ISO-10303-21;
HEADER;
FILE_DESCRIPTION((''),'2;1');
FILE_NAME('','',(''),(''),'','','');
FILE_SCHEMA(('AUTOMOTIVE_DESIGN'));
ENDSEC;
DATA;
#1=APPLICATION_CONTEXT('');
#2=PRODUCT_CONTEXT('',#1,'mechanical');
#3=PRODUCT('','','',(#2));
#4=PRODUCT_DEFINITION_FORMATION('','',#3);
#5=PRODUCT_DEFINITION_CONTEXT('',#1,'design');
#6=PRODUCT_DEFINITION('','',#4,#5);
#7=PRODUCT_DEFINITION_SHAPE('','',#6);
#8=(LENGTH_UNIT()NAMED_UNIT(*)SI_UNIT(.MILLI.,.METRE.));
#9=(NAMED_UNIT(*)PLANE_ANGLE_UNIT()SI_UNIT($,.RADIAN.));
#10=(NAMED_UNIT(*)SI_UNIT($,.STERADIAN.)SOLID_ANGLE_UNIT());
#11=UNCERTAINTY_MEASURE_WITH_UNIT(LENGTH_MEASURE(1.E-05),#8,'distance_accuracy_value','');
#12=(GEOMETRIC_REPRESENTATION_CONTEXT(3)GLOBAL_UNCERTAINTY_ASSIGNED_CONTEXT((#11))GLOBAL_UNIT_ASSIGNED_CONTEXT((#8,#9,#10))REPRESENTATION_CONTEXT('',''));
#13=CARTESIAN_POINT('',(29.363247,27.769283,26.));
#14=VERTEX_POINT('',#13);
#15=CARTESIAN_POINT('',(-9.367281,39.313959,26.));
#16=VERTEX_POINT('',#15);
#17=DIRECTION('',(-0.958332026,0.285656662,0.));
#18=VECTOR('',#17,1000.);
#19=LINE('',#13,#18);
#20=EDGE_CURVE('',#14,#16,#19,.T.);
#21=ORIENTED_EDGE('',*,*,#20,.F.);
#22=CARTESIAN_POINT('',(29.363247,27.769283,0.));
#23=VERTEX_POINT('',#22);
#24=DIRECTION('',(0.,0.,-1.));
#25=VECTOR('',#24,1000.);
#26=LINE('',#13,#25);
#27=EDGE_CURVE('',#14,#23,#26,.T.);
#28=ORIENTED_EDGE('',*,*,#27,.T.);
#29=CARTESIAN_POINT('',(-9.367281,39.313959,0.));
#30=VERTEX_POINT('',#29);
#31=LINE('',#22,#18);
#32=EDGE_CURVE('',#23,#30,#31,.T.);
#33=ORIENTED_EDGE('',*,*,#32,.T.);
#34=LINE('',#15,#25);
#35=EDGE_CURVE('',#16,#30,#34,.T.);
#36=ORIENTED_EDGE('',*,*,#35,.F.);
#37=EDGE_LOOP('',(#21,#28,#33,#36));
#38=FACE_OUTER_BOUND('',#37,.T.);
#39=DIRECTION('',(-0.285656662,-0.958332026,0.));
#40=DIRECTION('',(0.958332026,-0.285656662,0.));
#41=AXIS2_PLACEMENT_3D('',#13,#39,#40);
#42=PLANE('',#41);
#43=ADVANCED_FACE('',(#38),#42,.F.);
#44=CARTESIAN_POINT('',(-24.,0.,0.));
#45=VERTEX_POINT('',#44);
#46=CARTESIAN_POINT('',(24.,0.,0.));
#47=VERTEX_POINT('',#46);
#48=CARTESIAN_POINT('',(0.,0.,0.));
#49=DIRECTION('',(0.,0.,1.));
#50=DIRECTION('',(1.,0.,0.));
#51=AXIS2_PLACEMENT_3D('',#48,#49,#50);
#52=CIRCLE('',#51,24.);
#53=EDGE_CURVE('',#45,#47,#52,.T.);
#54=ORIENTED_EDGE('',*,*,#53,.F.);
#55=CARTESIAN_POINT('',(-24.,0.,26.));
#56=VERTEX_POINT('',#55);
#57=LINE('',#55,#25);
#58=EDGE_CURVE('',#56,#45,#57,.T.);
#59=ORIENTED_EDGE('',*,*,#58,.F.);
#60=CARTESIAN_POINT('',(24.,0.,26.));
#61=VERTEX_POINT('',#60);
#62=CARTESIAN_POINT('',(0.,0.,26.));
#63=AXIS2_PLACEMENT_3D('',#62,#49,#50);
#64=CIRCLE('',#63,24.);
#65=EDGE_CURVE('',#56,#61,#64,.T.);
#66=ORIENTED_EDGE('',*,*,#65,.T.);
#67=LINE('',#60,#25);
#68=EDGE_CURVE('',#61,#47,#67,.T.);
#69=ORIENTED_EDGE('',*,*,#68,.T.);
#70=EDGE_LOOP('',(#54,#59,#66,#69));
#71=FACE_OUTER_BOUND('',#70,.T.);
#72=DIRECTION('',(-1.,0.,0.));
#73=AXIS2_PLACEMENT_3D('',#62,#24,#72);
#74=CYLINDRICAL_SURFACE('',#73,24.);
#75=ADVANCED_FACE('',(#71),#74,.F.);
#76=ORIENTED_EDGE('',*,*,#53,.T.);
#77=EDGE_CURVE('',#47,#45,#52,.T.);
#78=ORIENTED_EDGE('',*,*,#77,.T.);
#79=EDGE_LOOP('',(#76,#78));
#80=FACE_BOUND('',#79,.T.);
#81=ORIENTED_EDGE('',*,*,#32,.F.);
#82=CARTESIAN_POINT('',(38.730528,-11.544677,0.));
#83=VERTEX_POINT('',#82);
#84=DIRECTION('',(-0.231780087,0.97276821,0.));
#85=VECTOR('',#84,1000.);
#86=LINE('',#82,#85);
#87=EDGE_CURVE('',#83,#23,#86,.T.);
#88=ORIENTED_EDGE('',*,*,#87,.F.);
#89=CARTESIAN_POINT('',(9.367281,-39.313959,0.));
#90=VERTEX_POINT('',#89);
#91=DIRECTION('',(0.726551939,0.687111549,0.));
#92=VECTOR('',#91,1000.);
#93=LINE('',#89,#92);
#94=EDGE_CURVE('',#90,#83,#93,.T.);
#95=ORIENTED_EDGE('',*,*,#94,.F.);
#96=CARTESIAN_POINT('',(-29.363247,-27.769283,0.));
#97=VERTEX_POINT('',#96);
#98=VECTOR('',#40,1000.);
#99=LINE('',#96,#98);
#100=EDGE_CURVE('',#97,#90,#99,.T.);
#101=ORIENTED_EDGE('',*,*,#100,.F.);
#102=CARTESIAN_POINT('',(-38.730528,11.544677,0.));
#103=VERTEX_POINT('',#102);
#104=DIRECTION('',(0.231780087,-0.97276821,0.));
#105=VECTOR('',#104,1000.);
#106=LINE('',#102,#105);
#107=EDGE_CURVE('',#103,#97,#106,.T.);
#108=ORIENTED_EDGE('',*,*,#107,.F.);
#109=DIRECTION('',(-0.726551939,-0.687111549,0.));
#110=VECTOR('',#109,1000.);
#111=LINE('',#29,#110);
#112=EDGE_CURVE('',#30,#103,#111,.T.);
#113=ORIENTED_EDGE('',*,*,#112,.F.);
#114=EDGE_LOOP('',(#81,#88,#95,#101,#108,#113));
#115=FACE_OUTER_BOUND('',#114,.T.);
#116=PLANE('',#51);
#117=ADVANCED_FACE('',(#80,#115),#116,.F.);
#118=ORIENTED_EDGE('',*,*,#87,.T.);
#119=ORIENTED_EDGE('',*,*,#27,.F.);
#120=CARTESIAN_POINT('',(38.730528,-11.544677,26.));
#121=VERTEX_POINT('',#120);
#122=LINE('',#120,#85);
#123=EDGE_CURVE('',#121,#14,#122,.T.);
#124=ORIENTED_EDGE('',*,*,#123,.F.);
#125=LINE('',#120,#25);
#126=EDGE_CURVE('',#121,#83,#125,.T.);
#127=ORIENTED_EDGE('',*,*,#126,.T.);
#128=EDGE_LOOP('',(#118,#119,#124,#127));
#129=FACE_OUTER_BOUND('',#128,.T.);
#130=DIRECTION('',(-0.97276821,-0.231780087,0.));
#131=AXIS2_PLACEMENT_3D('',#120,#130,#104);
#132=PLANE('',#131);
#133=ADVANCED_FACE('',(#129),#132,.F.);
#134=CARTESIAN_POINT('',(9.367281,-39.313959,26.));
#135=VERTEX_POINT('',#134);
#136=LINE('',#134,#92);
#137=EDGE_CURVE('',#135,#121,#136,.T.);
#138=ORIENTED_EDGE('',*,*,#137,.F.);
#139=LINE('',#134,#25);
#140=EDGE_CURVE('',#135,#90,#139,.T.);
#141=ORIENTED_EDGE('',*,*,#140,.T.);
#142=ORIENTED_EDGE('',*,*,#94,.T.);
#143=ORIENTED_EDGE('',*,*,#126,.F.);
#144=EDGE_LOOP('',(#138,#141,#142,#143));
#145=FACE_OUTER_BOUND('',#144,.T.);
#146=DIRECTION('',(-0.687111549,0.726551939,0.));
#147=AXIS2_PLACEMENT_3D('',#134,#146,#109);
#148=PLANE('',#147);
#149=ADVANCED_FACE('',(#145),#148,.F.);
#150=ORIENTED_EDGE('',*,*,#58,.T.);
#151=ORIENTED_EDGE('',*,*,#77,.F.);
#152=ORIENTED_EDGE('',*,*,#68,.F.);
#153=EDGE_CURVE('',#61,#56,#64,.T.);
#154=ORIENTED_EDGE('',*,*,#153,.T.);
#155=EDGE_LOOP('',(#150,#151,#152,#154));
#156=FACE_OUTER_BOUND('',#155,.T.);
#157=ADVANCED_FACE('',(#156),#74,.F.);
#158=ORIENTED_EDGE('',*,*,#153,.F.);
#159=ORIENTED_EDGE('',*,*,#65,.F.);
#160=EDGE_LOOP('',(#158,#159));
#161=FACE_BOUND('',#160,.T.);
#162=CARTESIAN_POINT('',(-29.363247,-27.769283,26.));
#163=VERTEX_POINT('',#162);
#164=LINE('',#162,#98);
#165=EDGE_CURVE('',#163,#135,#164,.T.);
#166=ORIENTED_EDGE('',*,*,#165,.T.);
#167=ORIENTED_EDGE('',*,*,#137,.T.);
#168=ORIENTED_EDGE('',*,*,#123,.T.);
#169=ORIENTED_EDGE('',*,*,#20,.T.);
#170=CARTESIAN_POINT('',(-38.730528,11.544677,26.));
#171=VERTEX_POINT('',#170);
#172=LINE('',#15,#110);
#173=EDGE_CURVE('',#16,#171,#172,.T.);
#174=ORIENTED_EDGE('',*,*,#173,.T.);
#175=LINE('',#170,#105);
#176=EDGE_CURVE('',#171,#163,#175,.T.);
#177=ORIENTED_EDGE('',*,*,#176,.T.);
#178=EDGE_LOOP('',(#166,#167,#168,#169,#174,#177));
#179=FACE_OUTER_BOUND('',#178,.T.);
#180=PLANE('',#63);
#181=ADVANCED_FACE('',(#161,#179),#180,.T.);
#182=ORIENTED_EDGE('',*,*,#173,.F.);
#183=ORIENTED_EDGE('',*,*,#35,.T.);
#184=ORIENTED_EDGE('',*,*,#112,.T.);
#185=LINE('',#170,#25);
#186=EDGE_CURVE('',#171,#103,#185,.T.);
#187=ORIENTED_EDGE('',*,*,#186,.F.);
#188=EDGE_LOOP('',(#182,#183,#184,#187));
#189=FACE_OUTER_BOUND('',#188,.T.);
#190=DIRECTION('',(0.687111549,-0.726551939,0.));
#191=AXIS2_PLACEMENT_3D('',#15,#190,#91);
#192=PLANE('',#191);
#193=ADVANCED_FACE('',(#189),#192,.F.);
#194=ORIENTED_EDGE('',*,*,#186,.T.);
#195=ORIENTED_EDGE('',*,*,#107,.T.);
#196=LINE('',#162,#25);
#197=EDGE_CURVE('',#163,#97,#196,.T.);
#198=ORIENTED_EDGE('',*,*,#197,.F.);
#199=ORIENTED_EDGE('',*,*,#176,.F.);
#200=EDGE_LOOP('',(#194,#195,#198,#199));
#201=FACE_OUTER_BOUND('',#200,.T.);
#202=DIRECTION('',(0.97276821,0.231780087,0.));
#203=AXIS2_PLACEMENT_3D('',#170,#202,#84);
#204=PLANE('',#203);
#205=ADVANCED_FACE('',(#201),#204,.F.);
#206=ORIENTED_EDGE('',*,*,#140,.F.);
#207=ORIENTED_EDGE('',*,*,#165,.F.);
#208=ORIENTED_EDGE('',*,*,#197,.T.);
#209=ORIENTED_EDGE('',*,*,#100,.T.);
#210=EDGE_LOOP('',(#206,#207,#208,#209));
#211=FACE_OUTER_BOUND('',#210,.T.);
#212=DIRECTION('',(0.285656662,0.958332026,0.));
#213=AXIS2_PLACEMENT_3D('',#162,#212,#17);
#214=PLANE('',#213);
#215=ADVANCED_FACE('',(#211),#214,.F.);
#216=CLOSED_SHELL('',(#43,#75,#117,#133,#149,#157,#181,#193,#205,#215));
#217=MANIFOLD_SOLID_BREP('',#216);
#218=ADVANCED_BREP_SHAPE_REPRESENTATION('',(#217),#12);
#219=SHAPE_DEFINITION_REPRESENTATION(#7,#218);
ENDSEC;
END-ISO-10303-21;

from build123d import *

# Parameters (mm, degrees)
SKETCH1_R           = 24
BOSS_EXTRUDE1_DEPTH = 26


with BuildPart() as part:
    # Sketch1 → Boss-Extrude1 (new body)
    with BuildSketch(Plane.XY):
        Polygon((38.730527716, -11.544676531), (29.363247012, 27.769282638), (-9.367280704, 39.313959169), (-38.730527716, 11.544676531), (-29.363247012, -27.769282638), (9.367280704, -39.313959169), align=None)
        with Locations(Location((0, 0, 0), (0, 0, 180))):
            Circle(SKETCH1_R, mode=Mode.SUBTRACT)
    extrude(amount=BOSS_EXTRUDE1_DEPTH)


solid = part.part
